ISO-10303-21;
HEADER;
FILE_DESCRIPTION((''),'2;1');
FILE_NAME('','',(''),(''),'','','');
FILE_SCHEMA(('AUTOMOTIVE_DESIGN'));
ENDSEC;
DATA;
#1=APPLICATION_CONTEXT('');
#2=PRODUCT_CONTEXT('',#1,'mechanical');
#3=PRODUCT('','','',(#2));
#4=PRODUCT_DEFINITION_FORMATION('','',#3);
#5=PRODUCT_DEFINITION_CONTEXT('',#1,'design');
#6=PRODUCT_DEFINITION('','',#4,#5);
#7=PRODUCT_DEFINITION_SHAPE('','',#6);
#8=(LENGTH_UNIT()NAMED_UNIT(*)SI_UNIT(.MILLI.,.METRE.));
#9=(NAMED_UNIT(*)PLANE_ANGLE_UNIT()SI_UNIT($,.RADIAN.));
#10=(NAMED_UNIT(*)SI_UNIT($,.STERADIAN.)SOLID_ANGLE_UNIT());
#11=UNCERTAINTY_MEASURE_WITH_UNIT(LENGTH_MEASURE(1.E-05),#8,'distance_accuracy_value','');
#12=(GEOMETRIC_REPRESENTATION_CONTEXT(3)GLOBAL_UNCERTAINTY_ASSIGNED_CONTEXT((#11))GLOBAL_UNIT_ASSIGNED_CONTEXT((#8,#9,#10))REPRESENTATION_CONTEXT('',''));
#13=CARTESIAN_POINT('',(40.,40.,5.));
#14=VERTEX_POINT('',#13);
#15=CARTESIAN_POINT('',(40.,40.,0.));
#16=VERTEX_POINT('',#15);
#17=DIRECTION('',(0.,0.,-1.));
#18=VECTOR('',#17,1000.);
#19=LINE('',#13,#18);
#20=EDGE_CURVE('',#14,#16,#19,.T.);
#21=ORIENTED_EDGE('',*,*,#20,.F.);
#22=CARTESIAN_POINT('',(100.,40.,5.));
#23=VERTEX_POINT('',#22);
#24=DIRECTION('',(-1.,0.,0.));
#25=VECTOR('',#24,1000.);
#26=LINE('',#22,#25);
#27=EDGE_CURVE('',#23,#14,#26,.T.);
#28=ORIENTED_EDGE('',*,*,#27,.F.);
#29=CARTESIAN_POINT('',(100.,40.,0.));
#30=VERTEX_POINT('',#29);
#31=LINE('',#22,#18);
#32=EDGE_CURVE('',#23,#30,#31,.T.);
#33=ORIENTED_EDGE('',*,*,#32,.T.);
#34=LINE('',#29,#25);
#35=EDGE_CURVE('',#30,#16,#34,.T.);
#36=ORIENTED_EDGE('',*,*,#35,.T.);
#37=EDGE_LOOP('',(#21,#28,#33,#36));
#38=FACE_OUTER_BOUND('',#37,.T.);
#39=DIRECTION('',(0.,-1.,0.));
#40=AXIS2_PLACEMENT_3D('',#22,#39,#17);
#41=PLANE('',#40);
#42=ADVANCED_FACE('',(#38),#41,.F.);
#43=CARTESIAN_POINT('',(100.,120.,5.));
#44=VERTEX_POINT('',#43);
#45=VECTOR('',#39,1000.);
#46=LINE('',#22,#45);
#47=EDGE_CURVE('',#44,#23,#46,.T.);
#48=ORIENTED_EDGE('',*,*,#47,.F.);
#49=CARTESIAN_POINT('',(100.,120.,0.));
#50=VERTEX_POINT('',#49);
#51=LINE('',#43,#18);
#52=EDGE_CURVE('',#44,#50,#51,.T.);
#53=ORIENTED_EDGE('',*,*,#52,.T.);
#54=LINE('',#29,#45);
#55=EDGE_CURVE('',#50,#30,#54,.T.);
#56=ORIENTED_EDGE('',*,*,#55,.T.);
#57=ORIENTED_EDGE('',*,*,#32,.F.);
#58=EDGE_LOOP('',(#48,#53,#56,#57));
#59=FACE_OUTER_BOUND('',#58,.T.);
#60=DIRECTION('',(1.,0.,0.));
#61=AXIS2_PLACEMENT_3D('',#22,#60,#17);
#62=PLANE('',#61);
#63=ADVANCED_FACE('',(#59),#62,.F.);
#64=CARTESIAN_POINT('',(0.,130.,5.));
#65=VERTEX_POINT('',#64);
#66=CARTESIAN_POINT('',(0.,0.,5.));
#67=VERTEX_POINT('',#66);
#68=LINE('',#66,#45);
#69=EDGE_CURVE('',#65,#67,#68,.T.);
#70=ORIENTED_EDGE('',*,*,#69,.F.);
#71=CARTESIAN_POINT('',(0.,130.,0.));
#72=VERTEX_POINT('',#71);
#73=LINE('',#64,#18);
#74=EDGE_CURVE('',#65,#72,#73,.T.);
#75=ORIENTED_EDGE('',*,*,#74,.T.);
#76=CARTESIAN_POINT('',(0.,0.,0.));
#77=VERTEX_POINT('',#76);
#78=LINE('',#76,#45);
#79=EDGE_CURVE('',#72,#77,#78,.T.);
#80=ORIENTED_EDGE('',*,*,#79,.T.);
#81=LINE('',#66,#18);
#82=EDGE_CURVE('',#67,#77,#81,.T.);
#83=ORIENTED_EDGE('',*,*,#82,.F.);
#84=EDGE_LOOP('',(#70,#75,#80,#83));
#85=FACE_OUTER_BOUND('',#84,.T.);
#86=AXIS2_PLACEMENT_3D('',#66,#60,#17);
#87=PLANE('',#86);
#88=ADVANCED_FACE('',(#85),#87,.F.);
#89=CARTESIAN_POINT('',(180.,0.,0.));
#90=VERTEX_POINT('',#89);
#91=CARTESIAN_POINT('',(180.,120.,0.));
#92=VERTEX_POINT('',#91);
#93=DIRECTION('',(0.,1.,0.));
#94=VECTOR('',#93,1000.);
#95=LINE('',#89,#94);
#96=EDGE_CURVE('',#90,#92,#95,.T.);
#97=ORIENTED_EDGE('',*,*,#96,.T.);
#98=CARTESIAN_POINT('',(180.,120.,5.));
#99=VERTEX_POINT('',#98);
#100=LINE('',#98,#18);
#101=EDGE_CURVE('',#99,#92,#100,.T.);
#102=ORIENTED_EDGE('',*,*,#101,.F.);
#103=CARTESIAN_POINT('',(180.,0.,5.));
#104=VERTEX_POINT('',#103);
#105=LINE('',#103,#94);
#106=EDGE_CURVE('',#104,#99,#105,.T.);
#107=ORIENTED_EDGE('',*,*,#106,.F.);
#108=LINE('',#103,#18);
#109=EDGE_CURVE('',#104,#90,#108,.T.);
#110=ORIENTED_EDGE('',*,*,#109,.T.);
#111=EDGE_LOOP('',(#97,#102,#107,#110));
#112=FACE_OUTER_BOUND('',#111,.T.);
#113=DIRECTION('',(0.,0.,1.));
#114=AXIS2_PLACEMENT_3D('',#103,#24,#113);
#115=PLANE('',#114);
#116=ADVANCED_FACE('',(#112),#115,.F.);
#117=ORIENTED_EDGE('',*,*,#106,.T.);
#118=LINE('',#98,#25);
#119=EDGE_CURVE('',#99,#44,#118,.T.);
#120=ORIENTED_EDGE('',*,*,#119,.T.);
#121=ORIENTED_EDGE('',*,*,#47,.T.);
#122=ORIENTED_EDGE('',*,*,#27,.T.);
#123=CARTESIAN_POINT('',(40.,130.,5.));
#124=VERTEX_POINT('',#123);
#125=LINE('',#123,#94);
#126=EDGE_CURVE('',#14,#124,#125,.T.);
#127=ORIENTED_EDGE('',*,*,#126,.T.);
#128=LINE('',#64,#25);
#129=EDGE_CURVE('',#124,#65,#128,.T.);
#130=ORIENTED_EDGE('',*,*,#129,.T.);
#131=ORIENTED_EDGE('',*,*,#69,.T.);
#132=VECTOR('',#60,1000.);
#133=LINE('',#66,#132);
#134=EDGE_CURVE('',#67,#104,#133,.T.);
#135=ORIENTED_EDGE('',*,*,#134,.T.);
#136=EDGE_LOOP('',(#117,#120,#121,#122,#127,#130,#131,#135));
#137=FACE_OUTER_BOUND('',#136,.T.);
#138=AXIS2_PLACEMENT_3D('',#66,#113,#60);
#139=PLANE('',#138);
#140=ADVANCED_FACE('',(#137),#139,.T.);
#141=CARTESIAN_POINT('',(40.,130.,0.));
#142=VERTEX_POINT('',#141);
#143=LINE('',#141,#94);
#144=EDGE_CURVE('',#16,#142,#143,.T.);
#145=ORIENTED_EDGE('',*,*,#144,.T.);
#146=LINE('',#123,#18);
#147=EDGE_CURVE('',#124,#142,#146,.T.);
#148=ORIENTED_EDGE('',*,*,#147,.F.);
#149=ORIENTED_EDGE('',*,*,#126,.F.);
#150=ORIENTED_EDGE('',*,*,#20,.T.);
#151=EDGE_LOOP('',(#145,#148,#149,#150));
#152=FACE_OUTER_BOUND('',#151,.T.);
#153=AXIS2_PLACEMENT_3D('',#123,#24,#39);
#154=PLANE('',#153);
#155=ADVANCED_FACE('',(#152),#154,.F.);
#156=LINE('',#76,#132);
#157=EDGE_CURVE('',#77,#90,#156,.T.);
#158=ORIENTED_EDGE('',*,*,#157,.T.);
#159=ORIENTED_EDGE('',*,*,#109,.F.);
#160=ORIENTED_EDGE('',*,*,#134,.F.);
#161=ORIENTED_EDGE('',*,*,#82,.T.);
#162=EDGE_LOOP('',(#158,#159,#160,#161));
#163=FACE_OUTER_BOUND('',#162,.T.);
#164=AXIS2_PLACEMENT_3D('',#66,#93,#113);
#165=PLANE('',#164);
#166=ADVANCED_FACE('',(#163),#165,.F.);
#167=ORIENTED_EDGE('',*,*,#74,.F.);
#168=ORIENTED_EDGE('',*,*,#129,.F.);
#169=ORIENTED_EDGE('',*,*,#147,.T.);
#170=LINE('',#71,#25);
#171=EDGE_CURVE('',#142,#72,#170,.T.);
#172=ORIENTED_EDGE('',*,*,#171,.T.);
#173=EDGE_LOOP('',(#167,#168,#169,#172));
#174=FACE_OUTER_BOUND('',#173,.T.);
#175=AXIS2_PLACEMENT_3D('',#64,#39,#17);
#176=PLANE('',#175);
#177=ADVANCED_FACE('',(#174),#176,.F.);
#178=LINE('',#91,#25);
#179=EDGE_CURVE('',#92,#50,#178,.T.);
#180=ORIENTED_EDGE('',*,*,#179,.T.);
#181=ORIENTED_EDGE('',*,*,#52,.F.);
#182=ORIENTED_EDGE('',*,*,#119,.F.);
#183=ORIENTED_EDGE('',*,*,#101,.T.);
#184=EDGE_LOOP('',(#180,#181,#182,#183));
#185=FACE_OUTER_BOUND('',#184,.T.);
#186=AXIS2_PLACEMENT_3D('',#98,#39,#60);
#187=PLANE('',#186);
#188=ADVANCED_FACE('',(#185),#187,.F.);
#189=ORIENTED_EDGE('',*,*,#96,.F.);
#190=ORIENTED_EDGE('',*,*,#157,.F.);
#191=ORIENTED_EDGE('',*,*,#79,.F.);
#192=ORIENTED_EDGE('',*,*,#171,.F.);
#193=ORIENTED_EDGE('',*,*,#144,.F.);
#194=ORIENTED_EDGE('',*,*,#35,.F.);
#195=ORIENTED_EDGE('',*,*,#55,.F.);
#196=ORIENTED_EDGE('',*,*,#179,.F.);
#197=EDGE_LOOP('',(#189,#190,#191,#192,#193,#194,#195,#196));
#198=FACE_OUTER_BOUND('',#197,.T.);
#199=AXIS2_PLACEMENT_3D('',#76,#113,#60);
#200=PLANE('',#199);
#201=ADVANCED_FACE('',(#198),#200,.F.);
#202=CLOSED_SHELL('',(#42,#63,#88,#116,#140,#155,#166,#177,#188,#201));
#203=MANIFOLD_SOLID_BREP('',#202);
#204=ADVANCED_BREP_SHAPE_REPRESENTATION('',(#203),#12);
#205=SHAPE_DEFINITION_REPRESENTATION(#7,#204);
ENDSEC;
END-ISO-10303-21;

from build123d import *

# Parameters (mm, degrees)
EXTRUDE_1_DEPTH = 5


with BuildPart() as part:
    # 草图1 → 凸台-拉伸1 (new body)
    with BuildSketch(Plane.XY):
        Polygon((0, 0), (0, 130), (40, 130), (40, 40), (100, 40), (100, 120), (180, 120), (180, 0), align=None)
    extrude(amount=EXTRUDE_1_DEPTH)


solid = part.part
